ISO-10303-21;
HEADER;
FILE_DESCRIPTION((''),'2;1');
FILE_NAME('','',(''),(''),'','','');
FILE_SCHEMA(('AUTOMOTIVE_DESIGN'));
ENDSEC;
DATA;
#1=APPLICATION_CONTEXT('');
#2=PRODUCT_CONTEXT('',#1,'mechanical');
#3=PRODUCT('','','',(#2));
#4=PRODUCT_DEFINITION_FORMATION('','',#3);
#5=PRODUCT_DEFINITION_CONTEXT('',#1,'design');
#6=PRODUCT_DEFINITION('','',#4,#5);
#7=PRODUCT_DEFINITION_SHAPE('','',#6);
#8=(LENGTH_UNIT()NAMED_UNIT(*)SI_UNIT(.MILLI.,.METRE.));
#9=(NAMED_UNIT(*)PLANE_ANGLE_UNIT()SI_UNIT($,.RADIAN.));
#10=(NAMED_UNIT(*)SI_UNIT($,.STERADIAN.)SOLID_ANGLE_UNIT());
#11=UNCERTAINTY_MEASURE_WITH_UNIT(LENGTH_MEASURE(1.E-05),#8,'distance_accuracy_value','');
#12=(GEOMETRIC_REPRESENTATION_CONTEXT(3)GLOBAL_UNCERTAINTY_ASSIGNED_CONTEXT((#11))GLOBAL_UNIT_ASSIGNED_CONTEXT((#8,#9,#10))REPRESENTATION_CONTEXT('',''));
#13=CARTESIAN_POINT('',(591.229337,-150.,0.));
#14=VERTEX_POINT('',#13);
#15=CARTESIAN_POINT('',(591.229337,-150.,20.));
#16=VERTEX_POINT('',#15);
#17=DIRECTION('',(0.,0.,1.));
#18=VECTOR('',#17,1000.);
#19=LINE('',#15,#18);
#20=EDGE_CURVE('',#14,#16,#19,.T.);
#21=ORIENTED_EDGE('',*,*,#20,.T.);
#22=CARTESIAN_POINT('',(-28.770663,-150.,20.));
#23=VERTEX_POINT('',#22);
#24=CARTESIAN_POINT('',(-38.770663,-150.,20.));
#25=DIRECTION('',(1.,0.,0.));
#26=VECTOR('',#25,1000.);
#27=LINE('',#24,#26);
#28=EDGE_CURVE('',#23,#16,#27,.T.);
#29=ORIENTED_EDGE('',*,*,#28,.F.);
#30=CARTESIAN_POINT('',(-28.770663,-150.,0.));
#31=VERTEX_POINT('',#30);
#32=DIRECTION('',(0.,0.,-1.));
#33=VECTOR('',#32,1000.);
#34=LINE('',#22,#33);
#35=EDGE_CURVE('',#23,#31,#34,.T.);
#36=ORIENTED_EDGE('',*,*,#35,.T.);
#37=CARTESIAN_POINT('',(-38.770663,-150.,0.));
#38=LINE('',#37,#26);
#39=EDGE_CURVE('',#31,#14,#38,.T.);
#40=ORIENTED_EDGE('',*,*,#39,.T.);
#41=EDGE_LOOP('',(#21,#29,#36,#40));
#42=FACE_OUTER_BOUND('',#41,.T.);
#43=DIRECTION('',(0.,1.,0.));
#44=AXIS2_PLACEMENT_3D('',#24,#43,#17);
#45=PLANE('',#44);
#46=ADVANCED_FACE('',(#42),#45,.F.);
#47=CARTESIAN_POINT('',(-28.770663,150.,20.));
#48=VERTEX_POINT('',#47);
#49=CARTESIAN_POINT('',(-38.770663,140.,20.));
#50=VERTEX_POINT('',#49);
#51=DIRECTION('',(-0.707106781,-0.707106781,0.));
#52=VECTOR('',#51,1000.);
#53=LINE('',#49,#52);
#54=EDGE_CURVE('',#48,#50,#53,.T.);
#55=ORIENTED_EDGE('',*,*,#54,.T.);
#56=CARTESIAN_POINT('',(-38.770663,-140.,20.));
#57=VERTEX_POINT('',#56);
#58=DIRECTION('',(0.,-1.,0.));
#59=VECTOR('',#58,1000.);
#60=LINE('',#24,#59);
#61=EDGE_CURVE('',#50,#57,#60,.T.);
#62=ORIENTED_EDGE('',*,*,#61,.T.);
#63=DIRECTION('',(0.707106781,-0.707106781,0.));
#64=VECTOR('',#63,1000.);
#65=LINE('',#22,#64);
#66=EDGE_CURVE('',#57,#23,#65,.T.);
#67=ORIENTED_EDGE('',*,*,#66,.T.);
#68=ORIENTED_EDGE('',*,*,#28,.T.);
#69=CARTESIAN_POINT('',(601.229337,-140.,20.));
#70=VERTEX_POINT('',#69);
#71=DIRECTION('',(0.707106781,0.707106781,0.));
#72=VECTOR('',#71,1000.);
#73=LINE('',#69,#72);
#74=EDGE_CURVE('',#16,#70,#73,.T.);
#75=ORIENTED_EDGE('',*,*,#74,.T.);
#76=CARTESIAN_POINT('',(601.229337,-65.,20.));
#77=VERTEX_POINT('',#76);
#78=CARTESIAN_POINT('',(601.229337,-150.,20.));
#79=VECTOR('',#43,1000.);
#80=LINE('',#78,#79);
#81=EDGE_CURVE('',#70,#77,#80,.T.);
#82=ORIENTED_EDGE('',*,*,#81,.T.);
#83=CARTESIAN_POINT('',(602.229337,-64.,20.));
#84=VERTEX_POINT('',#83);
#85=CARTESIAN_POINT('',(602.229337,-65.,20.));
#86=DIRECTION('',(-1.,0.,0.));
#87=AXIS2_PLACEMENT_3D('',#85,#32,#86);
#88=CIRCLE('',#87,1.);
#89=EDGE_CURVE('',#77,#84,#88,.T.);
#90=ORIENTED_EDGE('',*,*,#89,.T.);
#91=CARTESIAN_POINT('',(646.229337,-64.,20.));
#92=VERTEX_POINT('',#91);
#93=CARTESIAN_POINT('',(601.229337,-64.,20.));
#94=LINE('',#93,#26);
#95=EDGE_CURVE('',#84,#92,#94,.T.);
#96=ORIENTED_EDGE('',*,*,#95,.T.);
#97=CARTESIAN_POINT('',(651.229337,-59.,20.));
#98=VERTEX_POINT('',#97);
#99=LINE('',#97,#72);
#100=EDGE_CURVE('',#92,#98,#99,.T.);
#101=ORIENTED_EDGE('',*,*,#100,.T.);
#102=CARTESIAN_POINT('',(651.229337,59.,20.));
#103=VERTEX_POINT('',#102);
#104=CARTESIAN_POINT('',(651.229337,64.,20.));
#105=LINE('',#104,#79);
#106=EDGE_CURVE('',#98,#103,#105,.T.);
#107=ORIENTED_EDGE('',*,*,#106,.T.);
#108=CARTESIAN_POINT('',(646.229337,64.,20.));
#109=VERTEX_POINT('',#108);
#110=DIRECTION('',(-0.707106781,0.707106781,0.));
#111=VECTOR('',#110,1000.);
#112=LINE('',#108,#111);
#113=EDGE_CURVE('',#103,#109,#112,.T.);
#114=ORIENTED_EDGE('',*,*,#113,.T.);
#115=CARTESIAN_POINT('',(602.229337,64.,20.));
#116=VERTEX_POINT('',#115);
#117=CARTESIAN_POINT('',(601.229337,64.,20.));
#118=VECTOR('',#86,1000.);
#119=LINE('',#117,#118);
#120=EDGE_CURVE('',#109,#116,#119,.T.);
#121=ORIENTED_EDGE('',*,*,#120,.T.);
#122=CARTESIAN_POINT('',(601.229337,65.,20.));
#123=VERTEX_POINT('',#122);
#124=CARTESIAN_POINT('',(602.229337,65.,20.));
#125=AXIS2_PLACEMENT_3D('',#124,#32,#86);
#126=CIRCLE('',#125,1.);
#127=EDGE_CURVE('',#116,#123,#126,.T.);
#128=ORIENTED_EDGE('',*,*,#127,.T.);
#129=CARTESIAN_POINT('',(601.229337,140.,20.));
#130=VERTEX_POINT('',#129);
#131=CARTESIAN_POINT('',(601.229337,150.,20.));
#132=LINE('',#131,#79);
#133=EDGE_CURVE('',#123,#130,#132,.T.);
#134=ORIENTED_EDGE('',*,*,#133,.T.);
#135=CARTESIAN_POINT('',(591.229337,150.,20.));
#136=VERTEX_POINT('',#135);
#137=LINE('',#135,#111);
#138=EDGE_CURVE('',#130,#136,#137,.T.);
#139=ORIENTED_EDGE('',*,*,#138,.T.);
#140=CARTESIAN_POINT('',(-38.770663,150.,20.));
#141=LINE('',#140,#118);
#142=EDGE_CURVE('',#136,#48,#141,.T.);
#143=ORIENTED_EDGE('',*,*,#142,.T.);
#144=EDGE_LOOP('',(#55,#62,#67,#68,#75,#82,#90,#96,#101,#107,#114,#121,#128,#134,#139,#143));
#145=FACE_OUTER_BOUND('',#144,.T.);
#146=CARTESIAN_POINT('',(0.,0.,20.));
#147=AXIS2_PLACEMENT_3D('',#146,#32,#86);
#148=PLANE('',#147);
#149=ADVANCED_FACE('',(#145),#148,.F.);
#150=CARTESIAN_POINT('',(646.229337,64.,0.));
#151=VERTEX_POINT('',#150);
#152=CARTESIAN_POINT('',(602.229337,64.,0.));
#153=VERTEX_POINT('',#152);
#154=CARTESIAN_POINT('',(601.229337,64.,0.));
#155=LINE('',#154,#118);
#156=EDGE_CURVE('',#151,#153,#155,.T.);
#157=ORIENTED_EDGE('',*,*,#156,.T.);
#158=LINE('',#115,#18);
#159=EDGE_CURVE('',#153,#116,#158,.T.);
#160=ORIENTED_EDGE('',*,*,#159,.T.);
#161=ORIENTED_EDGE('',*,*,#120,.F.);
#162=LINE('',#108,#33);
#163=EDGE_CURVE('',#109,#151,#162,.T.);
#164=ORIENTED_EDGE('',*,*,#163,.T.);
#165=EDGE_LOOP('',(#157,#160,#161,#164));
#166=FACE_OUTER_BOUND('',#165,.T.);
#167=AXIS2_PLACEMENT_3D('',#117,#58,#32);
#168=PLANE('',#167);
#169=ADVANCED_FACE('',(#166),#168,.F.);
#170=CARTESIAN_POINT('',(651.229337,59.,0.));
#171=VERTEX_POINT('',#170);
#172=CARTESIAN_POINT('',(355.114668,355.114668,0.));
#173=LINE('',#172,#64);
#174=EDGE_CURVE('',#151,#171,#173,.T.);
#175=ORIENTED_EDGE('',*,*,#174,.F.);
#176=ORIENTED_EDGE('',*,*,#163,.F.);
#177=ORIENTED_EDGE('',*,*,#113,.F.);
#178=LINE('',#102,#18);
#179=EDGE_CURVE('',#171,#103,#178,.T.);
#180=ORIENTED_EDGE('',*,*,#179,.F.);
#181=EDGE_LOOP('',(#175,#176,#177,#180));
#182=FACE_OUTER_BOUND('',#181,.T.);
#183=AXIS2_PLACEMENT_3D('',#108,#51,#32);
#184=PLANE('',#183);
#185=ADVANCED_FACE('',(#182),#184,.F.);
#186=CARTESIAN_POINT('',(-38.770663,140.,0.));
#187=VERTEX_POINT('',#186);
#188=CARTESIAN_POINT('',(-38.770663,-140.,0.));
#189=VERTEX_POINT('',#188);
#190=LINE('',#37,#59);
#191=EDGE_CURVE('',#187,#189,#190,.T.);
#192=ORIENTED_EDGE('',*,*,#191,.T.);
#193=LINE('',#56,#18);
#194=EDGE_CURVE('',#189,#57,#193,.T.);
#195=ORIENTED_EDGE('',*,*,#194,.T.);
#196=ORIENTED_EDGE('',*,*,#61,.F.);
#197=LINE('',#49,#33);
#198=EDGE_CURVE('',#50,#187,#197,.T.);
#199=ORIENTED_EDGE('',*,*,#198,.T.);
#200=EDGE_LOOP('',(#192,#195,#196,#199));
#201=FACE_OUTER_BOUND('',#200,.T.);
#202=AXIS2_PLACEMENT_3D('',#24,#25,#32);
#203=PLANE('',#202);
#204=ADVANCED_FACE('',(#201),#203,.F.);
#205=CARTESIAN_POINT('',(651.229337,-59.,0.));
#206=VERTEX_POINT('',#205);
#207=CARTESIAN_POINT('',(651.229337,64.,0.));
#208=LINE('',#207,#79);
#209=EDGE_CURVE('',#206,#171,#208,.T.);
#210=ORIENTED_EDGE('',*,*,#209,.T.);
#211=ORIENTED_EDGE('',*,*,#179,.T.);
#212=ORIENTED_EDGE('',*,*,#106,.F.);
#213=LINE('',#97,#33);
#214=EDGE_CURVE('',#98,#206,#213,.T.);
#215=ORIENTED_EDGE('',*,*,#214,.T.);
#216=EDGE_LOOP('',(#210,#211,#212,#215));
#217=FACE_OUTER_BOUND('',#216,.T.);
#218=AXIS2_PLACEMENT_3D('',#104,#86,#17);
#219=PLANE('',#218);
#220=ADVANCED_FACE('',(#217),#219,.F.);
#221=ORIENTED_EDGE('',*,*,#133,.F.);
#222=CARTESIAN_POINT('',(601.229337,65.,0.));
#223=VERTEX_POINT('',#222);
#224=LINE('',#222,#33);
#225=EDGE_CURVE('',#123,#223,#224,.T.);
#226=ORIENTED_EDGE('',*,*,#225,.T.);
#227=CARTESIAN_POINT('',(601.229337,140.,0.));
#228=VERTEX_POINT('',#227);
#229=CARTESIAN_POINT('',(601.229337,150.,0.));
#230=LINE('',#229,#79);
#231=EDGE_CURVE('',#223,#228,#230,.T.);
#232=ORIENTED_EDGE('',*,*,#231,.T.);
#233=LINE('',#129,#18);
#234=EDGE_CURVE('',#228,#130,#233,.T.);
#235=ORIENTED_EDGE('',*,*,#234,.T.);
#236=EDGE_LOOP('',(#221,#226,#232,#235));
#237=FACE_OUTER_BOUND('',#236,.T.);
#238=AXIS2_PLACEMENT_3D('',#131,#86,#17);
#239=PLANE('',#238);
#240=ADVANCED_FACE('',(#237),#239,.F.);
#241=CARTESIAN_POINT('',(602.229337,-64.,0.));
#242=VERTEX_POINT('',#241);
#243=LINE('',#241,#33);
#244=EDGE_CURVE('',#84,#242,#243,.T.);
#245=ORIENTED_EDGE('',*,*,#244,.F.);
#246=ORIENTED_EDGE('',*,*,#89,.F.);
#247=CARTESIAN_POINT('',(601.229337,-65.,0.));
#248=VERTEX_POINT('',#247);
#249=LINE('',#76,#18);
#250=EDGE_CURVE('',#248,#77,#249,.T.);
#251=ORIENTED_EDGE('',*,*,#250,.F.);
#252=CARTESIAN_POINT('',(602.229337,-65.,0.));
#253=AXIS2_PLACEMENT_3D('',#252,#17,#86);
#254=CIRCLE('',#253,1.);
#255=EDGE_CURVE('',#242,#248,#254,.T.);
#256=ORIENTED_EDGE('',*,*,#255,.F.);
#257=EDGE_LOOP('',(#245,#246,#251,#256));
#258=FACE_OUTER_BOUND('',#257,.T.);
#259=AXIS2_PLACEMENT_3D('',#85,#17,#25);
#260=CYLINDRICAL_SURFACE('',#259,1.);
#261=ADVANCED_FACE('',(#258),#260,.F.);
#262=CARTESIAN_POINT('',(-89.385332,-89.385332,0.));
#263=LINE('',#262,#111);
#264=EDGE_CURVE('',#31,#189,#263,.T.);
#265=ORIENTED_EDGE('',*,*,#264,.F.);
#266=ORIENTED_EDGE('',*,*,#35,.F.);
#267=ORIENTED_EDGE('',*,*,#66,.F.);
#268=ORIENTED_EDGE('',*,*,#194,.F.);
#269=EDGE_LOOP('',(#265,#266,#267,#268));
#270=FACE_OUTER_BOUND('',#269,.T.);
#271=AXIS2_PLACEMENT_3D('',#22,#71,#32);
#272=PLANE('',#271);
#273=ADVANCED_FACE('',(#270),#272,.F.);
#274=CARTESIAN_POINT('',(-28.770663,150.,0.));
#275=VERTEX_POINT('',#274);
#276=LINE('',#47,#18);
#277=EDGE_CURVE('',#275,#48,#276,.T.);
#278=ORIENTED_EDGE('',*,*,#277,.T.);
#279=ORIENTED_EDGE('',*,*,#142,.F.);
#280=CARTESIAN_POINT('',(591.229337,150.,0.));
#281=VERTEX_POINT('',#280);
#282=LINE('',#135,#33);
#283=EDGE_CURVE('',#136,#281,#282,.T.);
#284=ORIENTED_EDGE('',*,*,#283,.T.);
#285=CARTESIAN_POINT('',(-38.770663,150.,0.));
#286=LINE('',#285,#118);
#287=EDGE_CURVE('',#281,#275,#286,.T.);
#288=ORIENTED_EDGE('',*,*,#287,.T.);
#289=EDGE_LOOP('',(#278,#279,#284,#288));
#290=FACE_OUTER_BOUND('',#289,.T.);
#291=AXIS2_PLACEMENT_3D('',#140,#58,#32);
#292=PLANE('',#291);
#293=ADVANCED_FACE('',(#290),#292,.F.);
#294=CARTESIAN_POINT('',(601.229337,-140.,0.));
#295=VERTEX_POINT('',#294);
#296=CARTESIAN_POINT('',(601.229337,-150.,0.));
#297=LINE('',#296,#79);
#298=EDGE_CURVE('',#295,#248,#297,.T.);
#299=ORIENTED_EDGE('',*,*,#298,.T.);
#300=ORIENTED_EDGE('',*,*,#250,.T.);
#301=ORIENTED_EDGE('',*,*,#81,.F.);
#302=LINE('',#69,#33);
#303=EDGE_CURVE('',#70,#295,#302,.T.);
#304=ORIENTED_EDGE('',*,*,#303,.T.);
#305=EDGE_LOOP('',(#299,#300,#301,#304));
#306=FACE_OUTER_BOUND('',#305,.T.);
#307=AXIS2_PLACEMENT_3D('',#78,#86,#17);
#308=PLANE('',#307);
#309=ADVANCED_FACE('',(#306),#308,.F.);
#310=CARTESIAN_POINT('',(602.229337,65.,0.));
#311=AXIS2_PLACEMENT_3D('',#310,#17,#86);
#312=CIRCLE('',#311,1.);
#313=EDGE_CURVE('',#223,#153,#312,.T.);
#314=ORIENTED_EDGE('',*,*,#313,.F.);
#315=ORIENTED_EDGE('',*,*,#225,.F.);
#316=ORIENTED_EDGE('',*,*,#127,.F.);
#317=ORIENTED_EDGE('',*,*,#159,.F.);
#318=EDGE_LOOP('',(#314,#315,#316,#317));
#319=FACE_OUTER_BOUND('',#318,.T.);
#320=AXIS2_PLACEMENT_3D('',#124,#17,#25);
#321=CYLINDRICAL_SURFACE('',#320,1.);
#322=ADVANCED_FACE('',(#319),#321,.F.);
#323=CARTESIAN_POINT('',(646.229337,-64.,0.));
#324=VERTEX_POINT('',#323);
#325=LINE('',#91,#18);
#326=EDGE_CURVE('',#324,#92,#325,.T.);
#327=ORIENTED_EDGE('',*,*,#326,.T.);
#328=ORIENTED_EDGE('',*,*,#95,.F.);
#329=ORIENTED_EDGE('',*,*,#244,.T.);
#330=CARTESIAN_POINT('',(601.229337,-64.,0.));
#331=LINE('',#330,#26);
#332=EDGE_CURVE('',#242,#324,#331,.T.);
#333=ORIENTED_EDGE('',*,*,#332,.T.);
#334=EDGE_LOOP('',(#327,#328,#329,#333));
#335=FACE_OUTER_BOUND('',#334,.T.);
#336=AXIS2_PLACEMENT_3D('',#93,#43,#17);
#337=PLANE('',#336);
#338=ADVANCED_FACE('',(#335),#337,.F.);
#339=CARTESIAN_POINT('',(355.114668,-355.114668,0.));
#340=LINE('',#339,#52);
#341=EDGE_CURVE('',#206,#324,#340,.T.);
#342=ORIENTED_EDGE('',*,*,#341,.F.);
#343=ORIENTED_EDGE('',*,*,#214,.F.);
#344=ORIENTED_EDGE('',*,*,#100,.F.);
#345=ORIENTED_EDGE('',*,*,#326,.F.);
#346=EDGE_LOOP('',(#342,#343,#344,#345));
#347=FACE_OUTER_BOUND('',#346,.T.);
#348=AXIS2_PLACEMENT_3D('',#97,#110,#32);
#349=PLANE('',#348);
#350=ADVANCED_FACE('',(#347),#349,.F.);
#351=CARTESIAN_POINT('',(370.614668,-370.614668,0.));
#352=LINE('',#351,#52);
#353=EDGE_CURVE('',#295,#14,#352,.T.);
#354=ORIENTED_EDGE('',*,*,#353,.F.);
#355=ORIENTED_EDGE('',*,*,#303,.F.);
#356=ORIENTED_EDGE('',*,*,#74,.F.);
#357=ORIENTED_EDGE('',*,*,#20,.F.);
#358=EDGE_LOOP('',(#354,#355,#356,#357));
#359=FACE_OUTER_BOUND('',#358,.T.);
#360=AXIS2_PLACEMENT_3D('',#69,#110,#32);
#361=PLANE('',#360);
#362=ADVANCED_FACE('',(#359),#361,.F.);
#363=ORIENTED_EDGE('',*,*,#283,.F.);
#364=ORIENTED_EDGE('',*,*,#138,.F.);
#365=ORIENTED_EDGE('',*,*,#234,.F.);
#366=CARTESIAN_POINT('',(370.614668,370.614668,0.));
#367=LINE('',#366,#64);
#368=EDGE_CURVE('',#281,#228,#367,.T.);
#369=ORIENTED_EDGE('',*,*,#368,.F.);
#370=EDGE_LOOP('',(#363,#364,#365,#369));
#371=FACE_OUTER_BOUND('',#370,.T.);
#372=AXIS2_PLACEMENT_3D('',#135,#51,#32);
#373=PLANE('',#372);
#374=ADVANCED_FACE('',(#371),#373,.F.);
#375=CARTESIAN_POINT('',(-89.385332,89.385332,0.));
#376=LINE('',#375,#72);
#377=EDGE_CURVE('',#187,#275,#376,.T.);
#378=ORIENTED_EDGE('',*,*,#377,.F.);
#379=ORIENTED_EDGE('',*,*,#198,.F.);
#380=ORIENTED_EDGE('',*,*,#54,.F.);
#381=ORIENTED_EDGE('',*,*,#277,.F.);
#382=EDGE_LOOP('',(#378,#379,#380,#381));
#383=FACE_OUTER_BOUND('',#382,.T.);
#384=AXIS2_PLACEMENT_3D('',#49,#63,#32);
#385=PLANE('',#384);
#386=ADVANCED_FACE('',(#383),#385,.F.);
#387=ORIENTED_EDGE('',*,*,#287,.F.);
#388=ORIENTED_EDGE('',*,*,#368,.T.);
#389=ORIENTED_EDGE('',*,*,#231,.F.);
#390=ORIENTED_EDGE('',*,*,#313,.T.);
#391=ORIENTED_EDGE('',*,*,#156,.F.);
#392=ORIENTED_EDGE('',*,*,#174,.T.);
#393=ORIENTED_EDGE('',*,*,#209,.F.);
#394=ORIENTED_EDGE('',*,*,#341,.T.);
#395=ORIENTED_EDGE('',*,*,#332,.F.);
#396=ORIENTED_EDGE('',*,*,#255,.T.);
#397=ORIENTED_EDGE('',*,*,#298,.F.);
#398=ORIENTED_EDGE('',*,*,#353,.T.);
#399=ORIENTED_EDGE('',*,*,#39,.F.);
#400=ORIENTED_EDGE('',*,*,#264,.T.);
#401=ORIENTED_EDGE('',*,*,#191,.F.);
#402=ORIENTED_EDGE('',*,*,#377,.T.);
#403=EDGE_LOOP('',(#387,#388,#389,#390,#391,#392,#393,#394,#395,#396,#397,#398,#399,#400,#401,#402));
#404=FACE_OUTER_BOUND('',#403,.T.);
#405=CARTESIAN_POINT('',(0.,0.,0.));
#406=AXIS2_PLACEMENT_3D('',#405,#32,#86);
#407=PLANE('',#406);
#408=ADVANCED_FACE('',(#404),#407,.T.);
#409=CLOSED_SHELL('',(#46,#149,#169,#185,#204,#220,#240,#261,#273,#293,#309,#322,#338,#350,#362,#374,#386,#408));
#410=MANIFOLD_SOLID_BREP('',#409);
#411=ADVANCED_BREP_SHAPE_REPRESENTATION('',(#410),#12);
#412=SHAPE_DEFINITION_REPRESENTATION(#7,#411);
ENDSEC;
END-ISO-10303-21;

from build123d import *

# Parameters (mm, degrees)
BOSS_EXTRUDE1_DEPTH = 20
CHAMFER1_SIZE       = 10
FILLET1_R           = 1
CHAMFER2_SIZE       = 5


with BuildPart() as part:
    # Sketch1 → Boss-Extrude1 (new body)
    with BuildSketch(Plane.XY):
        Polygon((-38.770663033, -150), (-38.770663033, 150), (601.229336967, 150), (601.229336967, 64), (651.229336967, 64), (651.229336967, -64), (601.229336967, -64), (601.229336967, -150), align=None)
    extrude(amount=BOSS_EXTRUDE1_DEPTH)

    # Chamfer1
    chamfer1_edges = [part.edges().sort_by_distance(p)[0] for p in [
        (601.229336967, 150, 10),
        (601.229336967, -150, 10),
        (-38.770663033, -150, 10),
        (-38.770663033, 150, 10),
    ]]
    chamfer(chamfer1_edges, length=CHAMFER1_SIZE)

    # Fillet1
    fillet1_edges = [part.edges().sort_by_distance(p)[0] for p in [
        (601.229336967, 64, 10),
        (601.229336967, -64, 10),
    ]]
    fillet(fillet1_edges, radius=FILLET1_R)

    # Chamfer2
    chamfer2_edges = [part.edges().sort_by_distance(p)[0] for p in [
        (651.229336967, 64, 10),
        (651.229336967, -64, 10),
    ]]
    chamfer(chamfer2_edges, length=CHAMFER2_SIZE)


solid = part.part
